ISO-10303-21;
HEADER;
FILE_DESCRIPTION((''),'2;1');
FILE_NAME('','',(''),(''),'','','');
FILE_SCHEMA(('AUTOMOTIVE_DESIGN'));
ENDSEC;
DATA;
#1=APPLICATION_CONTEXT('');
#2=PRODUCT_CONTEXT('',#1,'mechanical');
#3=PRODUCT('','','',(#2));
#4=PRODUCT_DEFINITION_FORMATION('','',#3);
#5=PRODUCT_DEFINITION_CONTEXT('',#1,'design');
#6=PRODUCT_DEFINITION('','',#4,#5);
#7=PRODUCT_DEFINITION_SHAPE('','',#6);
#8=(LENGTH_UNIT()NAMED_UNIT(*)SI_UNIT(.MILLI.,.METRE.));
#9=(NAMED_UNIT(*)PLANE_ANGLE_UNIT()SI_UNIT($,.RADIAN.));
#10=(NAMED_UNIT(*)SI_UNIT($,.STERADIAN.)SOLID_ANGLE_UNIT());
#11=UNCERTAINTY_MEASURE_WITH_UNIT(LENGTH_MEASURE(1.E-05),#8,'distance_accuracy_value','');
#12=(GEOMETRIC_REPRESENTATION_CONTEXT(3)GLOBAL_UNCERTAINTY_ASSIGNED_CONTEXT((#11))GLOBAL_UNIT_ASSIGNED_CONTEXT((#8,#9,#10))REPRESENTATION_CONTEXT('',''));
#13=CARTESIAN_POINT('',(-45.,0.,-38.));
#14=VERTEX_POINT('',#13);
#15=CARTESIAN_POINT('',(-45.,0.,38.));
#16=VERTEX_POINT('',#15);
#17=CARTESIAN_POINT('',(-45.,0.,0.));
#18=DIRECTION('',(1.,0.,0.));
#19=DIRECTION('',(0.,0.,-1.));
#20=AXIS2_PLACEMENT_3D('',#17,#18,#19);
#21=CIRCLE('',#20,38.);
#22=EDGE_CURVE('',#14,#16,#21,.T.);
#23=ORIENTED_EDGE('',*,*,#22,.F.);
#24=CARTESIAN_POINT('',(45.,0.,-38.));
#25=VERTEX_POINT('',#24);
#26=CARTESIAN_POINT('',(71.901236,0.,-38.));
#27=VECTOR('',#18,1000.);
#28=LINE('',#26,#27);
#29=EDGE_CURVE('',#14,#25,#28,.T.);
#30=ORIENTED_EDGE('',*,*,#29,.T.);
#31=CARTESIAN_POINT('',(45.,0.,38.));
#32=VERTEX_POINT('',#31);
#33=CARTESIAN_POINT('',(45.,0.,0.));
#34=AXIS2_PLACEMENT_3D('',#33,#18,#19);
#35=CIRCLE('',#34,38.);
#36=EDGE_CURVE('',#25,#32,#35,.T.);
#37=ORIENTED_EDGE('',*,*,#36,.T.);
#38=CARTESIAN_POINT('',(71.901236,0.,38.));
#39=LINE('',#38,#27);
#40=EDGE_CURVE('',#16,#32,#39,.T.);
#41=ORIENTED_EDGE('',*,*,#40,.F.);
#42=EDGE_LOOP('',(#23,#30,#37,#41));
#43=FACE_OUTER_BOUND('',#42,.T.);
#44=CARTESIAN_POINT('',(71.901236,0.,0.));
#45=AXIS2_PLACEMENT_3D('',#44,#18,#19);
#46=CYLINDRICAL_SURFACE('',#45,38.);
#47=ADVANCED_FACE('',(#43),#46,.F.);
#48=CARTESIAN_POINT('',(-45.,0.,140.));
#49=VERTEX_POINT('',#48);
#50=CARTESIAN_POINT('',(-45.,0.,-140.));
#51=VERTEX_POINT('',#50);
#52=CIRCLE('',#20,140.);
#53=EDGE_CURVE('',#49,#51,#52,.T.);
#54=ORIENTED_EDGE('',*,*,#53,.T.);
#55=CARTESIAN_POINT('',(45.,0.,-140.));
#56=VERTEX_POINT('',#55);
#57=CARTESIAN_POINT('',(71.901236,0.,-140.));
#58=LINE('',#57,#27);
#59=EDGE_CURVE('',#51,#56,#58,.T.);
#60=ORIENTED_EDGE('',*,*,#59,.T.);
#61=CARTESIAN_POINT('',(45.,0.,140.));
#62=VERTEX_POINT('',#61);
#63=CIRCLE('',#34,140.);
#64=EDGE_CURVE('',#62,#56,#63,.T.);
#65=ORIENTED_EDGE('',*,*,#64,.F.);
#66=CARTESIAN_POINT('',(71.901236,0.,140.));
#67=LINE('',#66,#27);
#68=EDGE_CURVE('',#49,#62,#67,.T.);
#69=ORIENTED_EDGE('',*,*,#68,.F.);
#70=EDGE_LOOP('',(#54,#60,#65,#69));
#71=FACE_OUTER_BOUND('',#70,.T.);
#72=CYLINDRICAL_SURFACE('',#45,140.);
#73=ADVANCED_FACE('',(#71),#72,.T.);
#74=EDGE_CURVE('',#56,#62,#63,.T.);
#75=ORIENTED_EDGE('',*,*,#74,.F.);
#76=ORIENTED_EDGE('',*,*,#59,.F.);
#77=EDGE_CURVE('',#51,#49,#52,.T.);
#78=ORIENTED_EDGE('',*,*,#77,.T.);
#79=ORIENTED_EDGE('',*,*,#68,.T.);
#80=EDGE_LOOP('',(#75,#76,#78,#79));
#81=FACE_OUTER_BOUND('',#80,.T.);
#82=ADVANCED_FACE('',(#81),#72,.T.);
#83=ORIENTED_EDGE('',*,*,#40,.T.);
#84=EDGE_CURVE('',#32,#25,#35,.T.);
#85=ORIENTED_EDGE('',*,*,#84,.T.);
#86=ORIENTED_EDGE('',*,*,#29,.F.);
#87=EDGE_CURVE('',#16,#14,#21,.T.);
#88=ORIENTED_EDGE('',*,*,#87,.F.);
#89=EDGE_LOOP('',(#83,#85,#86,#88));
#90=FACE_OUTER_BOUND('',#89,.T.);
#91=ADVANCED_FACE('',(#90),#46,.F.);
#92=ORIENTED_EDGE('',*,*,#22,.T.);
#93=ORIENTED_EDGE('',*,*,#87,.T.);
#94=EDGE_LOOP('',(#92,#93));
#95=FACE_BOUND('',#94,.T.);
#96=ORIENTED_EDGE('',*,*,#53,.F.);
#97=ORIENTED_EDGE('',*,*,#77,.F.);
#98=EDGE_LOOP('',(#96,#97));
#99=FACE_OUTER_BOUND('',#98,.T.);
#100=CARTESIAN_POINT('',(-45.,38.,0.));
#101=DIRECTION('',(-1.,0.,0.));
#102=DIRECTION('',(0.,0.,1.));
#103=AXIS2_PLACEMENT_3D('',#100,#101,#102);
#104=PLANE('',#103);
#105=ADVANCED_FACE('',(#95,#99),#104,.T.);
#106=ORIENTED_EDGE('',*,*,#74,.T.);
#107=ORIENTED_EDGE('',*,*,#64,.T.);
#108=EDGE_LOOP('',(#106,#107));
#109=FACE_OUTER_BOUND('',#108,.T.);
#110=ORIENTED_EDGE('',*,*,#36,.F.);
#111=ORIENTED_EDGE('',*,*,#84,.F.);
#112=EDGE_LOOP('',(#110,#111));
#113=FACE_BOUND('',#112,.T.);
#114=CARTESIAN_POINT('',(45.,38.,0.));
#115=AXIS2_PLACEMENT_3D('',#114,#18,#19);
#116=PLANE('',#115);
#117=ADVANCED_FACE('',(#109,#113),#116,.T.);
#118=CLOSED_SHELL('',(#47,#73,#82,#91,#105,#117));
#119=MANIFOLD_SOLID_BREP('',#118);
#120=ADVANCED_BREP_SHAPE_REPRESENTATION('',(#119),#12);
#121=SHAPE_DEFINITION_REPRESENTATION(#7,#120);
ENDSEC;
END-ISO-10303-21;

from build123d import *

# Parameters (mm, degrees)
SKETCH1_W = 90
SKETCH1_H = 102


with BuildPart() as part:
    # Sketch1 → Revolve1 (revolve)
    with BuildSketch(Plane.XY, mode=Mode.PRIVATE) as revolve1_sk:
        with Locations((0, 89)):
            Rectangle(SKETCH1_W, SKETCH1_H)
    revolve(revolve1_sk.sketch.rotate(Axis((71.901236476, 0, 0), (-1, 0, 0)), 90), axis=Axis((71.901236476, 0, 0), (-1, 0, 0)))


solid = part.part
